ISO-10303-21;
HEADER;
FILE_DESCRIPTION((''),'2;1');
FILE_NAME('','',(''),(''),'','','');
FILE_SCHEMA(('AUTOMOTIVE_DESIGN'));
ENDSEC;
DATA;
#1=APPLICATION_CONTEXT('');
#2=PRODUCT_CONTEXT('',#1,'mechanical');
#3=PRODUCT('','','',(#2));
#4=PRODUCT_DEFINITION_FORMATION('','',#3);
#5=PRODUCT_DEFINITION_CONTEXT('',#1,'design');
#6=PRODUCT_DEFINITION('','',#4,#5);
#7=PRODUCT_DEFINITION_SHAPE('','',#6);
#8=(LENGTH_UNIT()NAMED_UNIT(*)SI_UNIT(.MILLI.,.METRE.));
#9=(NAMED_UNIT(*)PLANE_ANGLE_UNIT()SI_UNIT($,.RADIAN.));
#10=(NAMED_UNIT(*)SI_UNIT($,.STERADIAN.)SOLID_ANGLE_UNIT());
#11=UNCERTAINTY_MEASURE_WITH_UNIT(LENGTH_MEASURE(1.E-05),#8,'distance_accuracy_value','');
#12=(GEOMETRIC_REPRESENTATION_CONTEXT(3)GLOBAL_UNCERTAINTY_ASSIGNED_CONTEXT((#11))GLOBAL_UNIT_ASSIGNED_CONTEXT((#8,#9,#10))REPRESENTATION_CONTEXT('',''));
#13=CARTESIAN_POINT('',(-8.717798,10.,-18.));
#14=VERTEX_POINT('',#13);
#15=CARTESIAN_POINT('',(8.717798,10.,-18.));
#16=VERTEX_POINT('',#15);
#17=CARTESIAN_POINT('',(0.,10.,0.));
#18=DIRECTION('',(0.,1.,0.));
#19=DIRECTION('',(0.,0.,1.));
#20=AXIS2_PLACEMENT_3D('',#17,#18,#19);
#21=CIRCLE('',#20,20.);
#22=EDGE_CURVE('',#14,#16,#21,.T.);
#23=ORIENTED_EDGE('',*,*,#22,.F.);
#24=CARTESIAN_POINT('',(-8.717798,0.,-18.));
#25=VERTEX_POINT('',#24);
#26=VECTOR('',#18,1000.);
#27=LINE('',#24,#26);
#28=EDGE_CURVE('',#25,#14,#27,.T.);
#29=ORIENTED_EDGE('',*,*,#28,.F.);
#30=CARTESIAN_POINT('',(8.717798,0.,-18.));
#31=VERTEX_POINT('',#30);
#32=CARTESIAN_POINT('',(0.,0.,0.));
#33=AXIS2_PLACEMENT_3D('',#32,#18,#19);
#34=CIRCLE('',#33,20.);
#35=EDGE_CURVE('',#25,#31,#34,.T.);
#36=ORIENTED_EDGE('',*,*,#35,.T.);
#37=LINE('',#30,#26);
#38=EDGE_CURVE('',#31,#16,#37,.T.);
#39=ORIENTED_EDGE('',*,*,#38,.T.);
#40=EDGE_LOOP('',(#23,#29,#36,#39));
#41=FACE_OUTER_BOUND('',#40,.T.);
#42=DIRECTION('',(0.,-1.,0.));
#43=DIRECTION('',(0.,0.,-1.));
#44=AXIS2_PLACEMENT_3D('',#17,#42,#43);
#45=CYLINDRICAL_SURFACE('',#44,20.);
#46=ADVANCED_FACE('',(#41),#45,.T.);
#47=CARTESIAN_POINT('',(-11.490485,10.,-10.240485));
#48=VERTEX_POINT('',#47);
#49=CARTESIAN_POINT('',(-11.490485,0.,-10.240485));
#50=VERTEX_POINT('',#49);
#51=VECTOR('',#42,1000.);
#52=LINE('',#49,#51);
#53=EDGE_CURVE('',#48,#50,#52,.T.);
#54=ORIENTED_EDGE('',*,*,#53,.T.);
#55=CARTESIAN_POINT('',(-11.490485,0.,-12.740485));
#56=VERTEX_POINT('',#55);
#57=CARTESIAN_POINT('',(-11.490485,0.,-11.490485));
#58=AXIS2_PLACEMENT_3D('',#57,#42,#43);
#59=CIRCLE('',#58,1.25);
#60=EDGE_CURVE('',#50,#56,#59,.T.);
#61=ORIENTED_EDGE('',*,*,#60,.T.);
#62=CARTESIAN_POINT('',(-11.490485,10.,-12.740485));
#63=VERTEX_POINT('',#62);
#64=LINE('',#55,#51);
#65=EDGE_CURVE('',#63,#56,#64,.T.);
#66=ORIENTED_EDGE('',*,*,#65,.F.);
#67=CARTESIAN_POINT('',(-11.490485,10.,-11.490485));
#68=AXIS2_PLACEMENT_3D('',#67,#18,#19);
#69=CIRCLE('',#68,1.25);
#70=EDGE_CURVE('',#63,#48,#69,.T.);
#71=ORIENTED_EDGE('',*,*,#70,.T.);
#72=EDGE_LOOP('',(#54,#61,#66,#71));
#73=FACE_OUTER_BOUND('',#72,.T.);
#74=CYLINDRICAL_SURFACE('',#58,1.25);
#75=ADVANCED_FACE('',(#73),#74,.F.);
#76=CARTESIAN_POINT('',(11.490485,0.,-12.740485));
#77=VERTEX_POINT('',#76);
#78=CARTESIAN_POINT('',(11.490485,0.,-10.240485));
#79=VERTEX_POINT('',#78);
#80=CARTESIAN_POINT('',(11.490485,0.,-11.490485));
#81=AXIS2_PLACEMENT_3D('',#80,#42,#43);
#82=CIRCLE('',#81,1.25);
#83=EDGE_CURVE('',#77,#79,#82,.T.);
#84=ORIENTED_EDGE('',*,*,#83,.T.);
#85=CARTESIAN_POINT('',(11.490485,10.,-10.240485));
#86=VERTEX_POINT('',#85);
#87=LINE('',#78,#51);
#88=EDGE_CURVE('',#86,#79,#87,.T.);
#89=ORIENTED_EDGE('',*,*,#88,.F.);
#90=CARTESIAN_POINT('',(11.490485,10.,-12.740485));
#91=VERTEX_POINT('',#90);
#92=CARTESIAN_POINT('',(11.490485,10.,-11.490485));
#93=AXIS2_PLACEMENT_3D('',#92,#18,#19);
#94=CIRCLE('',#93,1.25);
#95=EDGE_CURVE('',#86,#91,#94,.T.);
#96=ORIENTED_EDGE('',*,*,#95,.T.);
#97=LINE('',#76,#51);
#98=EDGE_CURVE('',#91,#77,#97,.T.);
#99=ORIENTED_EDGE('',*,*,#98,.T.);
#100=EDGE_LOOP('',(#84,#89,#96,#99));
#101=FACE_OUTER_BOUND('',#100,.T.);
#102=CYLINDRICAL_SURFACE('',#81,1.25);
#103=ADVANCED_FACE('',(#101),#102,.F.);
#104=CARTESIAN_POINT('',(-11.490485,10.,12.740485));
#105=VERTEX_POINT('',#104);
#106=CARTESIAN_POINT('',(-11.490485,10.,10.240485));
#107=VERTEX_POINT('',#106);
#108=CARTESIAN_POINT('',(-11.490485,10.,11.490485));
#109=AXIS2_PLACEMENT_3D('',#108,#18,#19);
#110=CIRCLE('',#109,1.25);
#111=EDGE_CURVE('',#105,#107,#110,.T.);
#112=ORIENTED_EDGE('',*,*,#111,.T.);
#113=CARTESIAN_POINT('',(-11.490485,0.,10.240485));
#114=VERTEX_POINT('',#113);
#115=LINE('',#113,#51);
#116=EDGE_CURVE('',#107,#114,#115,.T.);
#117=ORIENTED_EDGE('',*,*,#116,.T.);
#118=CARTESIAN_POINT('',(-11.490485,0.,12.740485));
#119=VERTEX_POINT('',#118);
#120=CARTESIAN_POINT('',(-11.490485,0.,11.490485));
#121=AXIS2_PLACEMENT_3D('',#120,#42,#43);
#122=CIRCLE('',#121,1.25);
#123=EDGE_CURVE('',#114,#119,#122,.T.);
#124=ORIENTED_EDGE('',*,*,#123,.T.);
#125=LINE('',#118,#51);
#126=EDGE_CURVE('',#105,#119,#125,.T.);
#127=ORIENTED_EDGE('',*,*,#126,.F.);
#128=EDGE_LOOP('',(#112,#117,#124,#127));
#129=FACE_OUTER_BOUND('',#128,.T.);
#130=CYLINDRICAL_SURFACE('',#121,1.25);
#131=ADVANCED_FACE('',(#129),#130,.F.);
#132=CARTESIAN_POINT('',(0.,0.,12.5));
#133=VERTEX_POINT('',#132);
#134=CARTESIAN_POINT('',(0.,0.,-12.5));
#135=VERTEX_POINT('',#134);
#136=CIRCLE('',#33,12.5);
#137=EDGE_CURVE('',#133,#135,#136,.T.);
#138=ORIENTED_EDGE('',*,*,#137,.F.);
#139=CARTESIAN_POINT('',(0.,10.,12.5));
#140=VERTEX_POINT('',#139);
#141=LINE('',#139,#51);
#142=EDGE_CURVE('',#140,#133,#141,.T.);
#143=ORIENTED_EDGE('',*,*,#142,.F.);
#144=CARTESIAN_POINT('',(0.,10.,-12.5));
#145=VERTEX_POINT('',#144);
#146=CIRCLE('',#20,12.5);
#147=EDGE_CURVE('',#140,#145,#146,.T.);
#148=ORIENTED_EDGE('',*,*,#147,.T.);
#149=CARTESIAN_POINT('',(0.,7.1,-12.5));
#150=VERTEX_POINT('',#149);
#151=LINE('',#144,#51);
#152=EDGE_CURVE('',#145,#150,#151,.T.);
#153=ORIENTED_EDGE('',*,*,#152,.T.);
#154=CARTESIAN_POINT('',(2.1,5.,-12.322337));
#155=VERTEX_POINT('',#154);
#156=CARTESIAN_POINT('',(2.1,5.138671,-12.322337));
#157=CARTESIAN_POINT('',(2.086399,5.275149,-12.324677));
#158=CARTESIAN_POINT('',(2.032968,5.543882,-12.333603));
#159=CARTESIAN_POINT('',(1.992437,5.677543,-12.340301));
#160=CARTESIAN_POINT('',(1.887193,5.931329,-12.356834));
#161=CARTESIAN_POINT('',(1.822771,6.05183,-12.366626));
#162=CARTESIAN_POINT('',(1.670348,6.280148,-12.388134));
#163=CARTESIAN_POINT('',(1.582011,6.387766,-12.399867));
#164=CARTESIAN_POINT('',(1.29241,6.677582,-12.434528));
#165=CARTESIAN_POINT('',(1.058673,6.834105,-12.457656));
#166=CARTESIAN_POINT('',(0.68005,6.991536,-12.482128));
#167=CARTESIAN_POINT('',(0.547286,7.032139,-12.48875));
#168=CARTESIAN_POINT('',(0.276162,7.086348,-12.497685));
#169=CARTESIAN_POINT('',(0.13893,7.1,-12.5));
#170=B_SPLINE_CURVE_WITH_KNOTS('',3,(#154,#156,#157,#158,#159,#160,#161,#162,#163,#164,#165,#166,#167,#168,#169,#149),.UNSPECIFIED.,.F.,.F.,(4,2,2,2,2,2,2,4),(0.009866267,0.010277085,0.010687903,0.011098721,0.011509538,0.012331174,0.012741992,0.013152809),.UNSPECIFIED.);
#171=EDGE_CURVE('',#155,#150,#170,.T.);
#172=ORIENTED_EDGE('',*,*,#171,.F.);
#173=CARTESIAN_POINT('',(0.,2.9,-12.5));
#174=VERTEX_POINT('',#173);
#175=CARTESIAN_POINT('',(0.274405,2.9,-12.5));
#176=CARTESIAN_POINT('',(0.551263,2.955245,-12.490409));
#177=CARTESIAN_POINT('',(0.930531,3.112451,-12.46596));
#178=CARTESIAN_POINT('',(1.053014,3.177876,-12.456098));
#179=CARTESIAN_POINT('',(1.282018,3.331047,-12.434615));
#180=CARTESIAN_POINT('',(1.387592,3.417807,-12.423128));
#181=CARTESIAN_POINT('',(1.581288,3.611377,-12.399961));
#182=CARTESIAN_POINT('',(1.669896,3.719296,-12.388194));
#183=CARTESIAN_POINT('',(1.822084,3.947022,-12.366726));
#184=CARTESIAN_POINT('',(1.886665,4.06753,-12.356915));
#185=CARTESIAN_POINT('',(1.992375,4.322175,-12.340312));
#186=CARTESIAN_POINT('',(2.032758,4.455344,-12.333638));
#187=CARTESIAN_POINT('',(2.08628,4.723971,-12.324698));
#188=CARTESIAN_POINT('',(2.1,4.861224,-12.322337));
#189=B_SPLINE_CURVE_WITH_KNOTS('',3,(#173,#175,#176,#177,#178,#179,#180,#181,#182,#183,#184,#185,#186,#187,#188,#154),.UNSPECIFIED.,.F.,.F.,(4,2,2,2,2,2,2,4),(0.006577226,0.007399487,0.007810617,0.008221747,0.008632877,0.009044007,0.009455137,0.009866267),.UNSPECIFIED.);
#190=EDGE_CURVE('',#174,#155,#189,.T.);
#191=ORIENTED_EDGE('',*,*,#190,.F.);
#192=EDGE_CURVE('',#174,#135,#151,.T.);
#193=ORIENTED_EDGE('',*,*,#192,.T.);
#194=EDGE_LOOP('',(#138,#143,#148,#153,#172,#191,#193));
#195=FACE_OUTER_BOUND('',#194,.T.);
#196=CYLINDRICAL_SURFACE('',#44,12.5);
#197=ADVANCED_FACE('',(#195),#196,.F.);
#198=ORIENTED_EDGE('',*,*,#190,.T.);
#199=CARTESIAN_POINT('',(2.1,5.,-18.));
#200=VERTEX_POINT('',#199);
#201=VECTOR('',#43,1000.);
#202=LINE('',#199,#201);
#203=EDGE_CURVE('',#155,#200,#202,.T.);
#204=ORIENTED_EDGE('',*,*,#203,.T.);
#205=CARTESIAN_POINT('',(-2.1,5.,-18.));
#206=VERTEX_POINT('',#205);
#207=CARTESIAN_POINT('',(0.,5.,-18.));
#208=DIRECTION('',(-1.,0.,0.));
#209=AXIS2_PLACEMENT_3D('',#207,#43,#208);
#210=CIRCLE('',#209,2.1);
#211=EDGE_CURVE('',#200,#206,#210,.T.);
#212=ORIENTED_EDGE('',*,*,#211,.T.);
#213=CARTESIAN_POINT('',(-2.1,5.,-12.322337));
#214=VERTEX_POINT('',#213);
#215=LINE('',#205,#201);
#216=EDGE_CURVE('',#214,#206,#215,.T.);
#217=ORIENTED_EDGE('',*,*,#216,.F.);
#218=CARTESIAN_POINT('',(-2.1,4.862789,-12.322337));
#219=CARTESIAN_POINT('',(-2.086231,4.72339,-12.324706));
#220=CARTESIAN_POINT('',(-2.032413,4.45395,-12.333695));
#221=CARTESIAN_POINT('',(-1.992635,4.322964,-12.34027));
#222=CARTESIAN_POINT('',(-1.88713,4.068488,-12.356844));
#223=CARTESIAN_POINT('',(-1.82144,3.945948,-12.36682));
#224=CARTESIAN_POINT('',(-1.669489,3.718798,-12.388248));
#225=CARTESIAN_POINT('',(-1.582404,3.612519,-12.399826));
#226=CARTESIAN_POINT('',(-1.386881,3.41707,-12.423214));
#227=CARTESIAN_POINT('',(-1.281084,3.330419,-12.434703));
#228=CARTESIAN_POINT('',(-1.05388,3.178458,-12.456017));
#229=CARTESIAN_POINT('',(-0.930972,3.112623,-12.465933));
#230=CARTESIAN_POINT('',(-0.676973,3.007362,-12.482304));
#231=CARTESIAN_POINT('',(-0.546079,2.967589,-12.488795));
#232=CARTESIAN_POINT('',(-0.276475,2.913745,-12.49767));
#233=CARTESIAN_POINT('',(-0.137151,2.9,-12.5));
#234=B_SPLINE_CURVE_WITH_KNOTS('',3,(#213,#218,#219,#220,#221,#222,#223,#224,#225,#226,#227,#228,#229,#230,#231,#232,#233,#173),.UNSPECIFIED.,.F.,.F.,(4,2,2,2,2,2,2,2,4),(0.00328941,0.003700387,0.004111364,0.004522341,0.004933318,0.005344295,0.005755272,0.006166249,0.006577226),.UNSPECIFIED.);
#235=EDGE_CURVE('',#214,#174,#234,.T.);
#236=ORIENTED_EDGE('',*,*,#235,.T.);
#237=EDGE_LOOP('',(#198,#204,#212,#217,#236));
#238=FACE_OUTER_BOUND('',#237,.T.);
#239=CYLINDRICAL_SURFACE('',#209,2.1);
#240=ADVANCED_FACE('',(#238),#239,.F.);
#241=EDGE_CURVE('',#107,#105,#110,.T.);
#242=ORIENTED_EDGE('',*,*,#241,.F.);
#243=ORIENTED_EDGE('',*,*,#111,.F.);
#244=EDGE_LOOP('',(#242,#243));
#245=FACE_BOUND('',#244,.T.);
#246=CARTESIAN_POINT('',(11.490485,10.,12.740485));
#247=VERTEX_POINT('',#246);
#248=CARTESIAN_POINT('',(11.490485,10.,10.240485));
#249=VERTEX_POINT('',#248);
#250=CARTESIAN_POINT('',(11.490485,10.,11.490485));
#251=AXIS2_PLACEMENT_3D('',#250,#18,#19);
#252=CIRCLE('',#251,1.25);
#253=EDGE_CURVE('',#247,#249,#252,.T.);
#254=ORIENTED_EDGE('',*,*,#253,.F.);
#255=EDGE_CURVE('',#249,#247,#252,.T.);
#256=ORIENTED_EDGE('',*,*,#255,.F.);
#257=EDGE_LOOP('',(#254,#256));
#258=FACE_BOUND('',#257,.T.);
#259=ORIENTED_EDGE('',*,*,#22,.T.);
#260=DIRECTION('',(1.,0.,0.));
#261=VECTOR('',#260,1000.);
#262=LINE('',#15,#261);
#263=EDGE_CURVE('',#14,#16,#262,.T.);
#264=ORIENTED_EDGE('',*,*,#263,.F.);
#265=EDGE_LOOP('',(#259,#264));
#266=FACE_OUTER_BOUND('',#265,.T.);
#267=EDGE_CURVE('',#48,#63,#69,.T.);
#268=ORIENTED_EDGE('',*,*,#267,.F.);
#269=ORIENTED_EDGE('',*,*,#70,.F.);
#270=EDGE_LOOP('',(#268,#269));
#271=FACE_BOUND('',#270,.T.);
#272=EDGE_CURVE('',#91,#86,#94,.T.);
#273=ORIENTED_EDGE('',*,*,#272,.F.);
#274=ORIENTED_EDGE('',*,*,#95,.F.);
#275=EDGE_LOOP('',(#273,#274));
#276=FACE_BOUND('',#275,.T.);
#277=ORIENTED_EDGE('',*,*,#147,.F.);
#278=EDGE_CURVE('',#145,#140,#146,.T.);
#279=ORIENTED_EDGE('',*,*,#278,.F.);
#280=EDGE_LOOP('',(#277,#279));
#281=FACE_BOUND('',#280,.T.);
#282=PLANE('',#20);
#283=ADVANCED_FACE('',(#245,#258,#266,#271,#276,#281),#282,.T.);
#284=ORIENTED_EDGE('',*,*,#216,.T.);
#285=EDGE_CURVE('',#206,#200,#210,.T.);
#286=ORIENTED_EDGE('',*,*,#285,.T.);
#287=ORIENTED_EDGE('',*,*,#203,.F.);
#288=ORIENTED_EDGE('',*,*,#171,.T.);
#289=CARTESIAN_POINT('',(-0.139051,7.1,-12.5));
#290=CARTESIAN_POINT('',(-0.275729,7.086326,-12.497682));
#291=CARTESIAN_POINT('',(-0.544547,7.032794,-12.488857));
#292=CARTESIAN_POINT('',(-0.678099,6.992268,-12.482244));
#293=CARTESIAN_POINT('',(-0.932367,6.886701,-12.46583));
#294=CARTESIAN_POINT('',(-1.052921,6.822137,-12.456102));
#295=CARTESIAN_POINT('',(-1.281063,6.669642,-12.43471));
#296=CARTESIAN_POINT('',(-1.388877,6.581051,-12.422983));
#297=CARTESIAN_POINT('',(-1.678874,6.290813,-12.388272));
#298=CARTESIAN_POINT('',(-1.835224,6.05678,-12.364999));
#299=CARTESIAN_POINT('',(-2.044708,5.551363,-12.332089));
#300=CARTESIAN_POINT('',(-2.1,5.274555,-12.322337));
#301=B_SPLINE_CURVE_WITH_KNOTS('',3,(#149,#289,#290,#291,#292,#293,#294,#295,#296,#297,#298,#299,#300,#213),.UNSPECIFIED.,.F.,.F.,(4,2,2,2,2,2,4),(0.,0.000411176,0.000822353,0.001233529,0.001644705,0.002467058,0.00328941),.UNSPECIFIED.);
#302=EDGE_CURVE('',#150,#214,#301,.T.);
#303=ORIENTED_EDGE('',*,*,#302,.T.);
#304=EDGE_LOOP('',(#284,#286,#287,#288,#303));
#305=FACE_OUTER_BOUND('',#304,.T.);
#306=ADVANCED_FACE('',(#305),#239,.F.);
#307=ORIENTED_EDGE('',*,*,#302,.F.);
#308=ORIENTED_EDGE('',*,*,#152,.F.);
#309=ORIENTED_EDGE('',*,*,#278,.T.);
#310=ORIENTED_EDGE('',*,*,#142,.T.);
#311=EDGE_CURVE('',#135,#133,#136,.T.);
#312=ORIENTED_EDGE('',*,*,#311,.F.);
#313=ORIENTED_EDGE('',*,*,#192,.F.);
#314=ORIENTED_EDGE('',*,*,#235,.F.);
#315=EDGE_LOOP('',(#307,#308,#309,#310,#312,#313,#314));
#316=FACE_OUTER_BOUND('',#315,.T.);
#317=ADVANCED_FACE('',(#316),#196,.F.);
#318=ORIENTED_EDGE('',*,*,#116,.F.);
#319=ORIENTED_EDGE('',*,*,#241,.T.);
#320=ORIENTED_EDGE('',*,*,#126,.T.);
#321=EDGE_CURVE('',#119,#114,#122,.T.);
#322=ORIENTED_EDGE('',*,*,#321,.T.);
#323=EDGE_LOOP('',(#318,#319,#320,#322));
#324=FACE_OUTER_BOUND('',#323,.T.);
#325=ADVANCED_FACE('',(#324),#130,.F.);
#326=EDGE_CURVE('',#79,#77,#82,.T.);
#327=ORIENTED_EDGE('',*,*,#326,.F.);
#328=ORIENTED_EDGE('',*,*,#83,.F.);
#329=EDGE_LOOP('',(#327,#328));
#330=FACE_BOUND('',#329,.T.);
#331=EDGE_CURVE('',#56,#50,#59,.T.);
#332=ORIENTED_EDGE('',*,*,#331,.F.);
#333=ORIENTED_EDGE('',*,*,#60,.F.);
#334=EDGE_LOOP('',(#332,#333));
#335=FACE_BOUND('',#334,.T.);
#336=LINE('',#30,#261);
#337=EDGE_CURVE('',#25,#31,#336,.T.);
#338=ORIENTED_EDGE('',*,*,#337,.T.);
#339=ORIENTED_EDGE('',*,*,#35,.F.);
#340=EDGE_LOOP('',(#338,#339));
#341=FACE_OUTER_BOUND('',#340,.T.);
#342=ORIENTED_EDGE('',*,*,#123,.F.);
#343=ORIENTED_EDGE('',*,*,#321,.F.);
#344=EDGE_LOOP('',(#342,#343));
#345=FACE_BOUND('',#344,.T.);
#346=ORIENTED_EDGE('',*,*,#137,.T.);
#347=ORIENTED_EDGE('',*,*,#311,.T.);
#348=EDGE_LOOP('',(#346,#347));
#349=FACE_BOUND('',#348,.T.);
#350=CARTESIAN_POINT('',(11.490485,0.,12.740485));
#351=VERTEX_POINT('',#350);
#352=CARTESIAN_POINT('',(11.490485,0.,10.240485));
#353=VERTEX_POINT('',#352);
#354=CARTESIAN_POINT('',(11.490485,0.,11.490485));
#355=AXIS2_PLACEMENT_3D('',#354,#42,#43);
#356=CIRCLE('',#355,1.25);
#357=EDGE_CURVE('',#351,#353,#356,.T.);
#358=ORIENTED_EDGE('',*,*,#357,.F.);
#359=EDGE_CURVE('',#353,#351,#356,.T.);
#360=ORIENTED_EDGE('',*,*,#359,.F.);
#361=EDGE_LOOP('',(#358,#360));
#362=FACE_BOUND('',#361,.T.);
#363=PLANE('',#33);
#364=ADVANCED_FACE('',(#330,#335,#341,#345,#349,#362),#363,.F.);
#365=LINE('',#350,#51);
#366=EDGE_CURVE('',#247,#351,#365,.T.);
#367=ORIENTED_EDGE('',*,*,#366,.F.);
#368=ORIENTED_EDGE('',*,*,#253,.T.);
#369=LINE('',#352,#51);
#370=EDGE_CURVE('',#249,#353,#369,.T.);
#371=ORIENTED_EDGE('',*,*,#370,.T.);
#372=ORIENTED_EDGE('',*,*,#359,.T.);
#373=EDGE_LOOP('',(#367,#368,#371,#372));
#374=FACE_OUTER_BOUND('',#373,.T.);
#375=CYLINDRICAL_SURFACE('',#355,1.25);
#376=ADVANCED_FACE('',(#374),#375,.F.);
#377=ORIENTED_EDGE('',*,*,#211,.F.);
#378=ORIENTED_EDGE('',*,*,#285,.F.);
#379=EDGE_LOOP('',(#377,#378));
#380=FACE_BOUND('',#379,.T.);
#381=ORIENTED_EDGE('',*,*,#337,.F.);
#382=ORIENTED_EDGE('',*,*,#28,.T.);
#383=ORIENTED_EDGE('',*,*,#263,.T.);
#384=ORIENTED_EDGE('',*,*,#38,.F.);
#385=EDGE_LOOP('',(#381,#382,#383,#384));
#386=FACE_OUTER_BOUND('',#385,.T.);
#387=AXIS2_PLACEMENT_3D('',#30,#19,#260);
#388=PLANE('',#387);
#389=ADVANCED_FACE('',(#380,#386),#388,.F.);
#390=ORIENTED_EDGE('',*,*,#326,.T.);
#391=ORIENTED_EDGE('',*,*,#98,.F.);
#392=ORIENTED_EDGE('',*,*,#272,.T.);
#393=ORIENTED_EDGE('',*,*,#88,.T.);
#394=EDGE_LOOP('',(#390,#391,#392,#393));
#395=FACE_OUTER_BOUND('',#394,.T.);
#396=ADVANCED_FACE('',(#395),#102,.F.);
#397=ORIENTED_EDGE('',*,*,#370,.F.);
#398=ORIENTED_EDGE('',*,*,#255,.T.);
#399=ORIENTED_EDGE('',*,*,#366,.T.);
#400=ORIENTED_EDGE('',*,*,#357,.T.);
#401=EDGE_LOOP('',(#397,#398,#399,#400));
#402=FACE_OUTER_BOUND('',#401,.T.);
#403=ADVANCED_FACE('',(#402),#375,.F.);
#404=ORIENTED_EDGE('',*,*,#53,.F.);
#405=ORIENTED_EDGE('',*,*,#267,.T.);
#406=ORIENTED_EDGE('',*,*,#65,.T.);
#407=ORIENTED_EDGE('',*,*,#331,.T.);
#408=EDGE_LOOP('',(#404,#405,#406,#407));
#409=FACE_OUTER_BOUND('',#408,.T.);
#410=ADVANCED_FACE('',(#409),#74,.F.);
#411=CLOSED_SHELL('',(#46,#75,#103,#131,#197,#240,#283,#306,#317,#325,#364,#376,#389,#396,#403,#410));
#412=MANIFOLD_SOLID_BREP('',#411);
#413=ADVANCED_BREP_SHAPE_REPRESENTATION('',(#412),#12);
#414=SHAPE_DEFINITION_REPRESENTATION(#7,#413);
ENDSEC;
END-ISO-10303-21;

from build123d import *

# Parameters (mm, degrees)
SKETCH1_R              = 20
SKETCH1_R_2            = 12.5
BOSS_EXTRUDE1_DEPTH    = 10
CUT_EXTRUDE1_DEPTH     = 31
M5_TAPPED_HOLE1_REACH  = 46.091
M5_TAPPED_HOLE1_BORE_R = 2.1
M3_TAPPED_HOLE1_D      = 2.5


with BuildPart() as part:
    # Sketch1 → Boss-Extrude1 (new body)
    with BuildSketch(Plane(origin=(0, 0, 0), x_dir=(1, 0, 0), z_dir=(0, 1, 0))):
        with Locations(Location((0, 0, 0), (0, 0, 270))):
            Circle(SKETCH1_R)
        with Locations(Location((0, 0, 0), (0, 0, 270))):
            Circle(SKETCH1_R_2, mode=Mode.SUBTRACT)
    extrude(amount=BOSS_EXTRUDE1_DEPTH)

    # Sketch2 → Cut-Extrude1 (cut, through all)
    with BuildSketch(Plane(origin=(0, 10, 0), x_dir=(1, 0, 0), z_dir=(0, 1, 0))):
        with BuildLine():
            Line((8.717797887, 18), (-8.717797887, 18))
            ThreePointArc((-8.717797887, 18), (0, 20), (8.717797887, 18))
        make_face()
    extrude(amount=-CUT_EXTRUDE1_DEPTH, mode=Mode.SUBTRACT)

    # M5 Tapped Hole1 bore → M5 Tapped Hole1 (cut, up to next)
    with BuildSketch(Plane(origin=(0, 0, -18), x_dir=(-1, 0, 0), z_dir=(0, 0, -1)), mode=Mode.PRIVATE) as m5_tapped_hole1_sk1:
        with Locations((0, 5)):
            Circle(M5_TAPPED_HOLE1_BORE_R)
    m5_tapped_hole1_tool1 = extrude(m5_tapped_hole1_sk1.sketch, amount=-M5_TAPPED_HOLE1_REACH, mode=Mode.PRIVATE) & part.part
    add(m5_tapped_hole1_tool1.solids().sort_by_distance((0, 5, -18))[0], mode=Mode.SUBTRACT)

    # M3 Tapped Hole1 (through all)
    with Locations(Plane(origin=(0, 0, 0), x_dir=(-1, 0, 0), z_dir=(0, -1, 0))):
        with Locations((-11.490485194, 11.490485194), (11.490485194, 11.490485194), (-11.490485194, -11.490485194), (11.490485194, -11.490485194)):
            Hole(M3_TAPPED_HOLE1_D / 2)


solid = part.part
